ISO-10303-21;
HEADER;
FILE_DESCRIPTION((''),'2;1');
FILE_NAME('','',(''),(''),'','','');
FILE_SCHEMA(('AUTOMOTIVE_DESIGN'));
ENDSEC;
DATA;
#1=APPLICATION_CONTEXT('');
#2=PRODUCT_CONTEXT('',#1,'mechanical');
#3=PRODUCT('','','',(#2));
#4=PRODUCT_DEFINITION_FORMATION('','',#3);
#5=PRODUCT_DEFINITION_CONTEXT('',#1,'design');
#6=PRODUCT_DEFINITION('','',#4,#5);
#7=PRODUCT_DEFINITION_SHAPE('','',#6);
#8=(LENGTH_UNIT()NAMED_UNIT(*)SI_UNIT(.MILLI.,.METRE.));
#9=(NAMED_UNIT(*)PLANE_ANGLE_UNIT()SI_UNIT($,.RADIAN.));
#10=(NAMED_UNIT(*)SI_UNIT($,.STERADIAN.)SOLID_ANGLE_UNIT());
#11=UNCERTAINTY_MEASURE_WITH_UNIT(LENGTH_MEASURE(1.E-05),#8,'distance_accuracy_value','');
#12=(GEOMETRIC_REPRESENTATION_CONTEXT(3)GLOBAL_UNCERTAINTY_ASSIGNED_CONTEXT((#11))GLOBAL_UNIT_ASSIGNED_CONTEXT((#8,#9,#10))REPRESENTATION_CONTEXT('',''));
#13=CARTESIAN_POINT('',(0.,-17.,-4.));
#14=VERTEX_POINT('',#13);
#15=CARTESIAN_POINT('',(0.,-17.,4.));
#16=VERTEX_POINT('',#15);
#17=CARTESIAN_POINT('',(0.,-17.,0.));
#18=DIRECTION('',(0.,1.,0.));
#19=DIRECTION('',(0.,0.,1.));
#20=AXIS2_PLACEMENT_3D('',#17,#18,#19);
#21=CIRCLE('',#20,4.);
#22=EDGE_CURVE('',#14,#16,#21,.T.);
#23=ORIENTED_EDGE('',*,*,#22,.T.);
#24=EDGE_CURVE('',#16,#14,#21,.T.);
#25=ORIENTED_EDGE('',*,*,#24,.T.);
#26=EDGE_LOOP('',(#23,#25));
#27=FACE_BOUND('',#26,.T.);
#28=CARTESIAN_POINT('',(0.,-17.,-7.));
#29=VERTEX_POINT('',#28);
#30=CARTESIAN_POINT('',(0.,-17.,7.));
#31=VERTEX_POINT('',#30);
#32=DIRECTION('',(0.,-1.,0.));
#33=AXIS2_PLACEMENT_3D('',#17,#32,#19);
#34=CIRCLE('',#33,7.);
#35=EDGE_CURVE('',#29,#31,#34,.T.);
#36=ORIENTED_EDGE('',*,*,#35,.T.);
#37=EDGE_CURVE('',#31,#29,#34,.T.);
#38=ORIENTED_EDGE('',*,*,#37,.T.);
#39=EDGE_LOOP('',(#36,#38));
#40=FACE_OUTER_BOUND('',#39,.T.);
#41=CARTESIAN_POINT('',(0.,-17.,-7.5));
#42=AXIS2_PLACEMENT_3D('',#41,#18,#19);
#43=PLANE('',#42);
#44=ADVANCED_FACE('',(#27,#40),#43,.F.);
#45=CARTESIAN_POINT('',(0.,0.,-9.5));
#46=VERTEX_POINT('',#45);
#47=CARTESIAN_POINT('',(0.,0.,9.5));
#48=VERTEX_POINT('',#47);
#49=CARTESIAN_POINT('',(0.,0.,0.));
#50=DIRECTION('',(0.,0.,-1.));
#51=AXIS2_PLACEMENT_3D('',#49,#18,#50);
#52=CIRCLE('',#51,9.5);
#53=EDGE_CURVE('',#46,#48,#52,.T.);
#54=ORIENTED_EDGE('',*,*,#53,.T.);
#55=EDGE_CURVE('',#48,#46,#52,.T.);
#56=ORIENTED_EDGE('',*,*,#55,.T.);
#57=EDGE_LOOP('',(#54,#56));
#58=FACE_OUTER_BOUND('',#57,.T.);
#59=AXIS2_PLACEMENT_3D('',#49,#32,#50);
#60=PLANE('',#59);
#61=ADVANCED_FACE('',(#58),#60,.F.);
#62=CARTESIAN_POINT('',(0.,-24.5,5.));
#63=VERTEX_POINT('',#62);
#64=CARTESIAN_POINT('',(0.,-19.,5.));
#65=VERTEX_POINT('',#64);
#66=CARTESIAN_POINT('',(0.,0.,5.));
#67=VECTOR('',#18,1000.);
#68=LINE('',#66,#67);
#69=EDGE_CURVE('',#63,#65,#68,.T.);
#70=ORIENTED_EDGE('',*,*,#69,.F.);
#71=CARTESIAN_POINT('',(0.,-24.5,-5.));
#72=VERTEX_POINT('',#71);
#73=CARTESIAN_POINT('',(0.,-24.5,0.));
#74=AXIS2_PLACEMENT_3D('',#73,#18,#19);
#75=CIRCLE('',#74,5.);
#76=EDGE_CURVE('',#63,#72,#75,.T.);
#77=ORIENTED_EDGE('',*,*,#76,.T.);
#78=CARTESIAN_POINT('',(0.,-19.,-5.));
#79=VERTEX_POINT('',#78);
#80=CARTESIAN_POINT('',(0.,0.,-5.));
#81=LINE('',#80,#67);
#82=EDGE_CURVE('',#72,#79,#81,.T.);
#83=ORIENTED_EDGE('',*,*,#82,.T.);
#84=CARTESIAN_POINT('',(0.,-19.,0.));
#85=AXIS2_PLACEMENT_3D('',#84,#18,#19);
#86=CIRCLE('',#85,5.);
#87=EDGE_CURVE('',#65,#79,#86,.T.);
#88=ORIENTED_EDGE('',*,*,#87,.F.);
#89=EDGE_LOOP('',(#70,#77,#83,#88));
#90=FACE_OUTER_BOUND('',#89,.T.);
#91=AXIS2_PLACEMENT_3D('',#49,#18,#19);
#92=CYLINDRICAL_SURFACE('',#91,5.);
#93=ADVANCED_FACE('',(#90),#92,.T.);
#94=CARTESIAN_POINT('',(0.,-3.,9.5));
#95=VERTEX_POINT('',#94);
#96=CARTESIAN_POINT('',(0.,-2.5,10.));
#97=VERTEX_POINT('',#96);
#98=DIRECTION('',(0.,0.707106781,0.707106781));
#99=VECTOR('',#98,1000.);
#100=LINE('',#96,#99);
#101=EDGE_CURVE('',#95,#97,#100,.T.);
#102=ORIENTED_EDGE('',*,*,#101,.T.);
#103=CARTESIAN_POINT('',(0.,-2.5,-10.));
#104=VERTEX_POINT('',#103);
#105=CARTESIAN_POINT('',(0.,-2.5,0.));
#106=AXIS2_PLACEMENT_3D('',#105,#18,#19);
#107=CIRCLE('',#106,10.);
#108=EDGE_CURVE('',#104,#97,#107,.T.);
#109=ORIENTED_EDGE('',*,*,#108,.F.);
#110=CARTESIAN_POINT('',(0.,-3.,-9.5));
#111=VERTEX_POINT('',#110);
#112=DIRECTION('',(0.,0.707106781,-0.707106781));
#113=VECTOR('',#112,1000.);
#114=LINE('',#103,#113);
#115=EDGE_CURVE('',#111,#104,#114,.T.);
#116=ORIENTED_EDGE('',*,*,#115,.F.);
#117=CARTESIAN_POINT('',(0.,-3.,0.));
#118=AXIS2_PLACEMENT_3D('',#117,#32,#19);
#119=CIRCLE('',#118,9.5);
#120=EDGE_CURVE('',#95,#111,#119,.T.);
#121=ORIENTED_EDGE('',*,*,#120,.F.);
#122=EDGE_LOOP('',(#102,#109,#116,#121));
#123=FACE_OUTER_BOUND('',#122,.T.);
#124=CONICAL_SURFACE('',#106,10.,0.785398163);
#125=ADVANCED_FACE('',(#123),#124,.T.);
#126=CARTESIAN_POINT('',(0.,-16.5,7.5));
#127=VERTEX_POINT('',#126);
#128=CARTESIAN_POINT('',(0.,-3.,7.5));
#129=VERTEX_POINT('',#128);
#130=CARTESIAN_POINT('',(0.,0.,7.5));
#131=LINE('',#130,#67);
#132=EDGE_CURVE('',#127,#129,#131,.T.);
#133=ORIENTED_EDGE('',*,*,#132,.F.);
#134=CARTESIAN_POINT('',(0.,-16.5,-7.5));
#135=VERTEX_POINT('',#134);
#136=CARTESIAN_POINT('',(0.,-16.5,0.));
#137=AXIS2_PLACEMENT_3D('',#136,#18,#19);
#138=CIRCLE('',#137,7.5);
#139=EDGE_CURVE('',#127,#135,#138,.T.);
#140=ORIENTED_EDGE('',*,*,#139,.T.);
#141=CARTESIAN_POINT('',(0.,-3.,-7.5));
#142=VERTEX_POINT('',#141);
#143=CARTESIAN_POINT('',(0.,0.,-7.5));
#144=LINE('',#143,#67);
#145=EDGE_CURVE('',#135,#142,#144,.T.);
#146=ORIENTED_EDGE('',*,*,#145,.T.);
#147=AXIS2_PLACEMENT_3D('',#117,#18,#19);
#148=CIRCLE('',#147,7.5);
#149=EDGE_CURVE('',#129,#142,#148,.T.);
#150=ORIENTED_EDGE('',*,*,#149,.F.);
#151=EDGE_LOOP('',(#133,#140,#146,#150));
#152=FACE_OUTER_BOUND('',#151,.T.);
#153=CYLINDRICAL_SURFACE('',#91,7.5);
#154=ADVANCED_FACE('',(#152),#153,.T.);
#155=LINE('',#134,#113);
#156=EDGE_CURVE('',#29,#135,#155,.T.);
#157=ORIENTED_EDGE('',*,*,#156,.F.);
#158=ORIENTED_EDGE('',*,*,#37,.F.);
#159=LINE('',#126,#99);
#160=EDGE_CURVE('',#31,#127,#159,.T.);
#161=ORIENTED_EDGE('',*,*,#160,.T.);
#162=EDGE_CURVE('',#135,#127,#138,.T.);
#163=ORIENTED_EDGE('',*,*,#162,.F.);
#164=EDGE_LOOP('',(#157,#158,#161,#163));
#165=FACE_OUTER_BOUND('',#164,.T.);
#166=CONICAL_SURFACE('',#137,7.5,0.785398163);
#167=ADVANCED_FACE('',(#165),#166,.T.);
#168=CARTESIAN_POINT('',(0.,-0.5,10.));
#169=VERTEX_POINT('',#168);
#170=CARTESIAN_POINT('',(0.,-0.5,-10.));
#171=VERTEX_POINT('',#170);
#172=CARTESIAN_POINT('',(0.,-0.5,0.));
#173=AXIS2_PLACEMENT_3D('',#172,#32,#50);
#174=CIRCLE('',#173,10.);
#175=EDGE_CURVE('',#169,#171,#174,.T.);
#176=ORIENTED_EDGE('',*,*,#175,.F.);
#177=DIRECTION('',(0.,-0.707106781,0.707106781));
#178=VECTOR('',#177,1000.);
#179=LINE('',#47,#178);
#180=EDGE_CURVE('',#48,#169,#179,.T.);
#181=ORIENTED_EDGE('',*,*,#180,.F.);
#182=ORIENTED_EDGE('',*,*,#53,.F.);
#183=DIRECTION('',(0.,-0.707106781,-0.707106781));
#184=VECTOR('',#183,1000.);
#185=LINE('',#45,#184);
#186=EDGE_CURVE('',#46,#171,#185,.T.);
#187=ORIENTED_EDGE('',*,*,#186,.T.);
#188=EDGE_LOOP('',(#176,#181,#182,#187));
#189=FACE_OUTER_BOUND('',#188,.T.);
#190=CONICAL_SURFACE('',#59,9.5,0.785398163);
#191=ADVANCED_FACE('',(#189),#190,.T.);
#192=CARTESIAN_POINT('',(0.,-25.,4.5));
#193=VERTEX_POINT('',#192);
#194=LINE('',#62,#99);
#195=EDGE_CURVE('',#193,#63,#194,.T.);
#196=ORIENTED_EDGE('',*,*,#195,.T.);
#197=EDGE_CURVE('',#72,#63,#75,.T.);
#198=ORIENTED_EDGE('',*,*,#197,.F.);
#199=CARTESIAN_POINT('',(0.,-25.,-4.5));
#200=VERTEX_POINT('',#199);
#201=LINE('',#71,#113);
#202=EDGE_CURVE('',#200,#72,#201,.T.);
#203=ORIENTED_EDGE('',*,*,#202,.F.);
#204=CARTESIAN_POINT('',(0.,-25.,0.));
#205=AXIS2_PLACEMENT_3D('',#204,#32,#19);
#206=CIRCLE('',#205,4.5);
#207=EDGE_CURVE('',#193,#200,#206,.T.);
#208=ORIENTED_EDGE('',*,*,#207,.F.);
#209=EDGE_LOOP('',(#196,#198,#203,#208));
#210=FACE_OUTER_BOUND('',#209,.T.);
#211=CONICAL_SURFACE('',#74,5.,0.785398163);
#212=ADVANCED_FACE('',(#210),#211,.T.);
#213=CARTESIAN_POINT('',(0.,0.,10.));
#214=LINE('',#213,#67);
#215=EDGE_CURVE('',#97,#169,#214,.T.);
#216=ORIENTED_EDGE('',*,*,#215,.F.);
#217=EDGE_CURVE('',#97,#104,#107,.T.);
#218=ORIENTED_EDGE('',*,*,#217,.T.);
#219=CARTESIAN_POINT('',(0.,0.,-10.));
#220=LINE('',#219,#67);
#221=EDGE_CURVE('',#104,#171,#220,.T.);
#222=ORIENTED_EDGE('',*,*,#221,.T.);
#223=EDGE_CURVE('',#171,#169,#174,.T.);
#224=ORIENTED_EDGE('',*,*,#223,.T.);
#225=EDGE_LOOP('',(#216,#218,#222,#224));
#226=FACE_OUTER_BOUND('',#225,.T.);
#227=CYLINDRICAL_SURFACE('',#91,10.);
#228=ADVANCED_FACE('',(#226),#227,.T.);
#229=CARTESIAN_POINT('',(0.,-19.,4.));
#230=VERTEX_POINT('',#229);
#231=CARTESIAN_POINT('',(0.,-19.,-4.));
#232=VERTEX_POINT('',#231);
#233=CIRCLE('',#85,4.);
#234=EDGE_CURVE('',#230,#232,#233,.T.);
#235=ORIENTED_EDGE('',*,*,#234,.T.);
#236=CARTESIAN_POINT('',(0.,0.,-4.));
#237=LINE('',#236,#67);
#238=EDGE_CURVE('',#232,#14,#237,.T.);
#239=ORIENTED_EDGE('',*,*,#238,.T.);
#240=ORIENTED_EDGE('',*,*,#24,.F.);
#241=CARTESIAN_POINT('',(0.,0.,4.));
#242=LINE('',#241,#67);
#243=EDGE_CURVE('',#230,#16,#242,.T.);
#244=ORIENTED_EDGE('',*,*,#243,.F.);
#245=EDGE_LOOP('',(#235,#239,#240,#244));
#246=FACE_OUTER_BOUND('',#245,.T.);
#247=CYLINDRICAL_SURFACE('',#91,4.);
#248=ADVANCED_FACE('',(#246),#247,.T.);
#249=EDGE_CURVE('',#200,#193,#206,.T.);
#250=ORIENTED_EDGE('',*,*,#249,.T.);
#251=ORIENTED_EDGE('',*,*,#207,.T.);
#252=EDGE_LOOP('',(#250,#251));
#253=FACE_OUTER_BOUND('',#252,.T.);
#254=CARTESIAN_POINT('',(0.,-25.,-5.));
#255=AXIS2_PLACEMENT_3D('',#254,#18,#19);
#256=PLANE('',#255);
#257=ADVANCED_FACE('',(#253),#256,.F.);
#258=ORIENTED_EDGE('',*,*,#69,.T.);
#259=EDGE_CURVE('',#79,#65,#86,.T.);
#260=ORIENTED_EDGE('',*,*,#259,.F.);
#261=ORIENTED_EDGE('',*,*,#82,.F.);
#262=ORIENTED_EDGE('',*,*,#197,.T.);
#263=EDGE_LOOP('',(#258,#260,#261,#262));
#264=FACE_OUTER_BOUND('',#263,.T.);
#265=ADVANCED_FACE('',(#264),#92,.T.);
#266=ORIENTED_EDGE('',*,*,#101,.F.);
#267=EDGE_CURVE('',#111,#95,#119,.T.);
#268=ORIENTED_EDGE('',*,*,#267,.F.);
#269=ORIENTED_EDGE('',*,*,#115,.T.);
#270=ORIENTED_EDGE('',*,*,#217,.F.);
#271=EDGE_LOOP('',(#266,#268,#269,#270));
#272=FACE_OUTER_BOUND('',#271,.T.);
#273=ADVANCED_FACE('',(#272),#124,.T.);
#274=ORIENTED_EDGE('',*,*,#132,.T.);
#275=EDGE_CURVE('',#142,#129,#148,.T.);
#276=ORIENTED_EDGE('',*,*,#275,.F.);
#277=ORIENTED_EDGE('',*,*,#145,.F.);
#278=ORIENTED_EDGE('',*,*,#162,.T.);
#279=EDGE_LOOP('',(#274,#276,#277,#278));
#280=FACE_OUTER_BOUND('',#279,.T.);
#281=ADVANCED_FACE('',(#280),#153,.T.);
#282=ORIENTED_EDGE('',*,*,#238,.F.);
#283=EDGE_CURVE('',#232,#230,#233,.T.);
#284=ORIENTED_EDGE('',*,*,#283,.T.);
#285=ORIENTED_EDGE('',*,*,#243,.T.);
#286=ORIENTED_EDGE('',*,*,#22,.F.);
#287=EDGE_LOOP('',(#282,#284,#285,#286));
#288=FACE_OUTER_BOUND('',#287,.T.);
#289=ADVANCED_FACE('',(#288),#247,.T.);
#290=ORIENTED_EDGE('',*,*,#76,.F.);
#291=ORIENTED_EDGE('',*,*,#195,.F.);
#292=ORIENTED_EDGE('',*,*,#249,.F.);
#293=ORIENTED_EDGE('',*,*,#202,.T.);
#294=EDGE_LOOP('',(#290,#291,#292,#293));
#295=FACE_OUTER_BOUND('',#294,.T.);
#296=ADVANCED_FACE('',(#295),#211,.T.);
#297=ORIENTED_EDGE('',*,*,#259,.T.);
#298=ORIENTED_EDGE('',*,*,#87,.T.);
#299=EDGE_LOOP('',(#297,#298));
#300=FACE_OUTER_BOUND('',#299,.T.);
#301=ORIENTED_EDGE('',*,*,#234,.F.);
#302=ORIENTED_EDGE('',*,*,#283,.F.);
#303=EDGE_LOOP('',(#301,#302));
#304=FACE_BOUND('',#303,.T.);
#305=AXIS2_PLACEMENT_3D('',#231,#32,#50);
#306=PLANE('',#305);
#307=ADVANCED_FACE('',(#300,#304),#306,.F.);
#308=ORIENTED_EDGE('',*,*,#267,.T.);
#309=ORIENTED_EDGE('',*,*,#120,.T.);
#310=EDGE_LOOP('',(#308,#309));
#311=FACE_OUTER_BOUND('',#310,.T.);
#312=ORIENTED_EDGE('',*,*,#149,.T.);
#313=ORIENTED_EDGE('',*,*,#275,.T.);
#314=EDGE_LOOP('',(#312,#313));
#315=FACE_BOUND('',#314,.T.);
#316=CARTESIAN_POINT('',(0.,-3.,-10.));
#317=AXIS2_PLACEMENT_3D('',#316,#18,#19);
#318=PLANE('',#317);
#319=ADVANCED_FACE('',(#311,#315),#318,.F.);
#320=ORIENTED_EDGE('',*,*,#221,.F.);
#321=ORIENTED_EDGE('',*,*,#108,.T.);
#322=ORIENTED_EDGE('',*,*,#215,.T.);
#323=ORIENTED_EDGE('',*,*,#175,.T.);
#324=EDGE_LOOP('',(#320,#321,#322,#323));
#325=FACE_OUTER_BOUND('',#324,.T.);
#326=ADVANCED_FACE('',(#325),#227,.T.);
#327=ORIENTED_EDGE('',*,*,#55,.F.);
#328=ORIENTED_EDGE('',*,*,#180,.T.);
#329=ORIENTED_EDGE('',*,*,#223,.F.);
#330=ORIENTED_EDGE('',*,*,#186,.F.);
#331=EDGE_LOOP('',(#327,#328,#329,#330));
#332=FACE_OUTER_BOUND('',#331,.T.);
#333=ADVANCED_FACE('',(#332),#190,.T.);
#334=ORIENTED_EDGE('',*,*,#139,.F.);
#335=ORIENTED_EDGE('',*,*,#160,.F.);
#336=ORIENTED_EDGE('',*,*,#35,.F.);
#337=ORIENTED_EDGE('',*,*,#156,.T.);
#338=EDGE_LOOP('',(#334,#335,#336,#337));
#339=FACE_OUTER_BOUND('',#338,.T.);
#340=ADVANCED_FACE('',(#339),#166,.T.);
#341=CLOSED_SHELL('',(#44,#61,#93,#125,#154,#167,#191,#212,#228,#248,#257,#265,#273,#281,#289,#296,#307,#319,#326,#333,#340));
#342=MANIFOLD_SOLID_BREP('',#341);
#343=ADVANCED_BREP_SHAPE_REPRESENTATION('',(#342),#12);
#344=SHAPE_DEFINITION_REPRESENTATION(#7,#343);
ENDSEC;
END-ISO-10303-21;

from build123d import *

# Parameters (mm, degrees)
CHAMFER1_SIZE = 0.5


with BuildPart() as part:
    # Sketch1 → Revolve1 (revolve)
    with BuildSketch(Plane(origin=(0, 0, 0), x_dir=(0, 0, -1), z_dir=(1, 0, 0)), mode=Mode.PRIVATE) as revolve1_sk:
        Polygon((0, 0), (10, 0), (10, -3), (7.5, -3), (7.5, -17), (4, -17), (4, -19), (5, -19), (5, -25), (0, -25), align=None)
    revolve(revolve1_sk.sketch.rotate(Axis((0, 0, 0), (0, -1, 0)), 180), axis=Axis((0, 0, 0), (0, -1, 0)))

    # Chamfer1
    chamfer1_edges = [part.edges().sort_by_distance(p)[0] for p in [
        (0, -17, -7.5),
        (0, -3, -10),
        (0, 0, -10),
        (0, -25, -5),
    ]]
    chamfer(chamfer1_edges, length=CHAMFER1_SIZE)


solid = part.part
